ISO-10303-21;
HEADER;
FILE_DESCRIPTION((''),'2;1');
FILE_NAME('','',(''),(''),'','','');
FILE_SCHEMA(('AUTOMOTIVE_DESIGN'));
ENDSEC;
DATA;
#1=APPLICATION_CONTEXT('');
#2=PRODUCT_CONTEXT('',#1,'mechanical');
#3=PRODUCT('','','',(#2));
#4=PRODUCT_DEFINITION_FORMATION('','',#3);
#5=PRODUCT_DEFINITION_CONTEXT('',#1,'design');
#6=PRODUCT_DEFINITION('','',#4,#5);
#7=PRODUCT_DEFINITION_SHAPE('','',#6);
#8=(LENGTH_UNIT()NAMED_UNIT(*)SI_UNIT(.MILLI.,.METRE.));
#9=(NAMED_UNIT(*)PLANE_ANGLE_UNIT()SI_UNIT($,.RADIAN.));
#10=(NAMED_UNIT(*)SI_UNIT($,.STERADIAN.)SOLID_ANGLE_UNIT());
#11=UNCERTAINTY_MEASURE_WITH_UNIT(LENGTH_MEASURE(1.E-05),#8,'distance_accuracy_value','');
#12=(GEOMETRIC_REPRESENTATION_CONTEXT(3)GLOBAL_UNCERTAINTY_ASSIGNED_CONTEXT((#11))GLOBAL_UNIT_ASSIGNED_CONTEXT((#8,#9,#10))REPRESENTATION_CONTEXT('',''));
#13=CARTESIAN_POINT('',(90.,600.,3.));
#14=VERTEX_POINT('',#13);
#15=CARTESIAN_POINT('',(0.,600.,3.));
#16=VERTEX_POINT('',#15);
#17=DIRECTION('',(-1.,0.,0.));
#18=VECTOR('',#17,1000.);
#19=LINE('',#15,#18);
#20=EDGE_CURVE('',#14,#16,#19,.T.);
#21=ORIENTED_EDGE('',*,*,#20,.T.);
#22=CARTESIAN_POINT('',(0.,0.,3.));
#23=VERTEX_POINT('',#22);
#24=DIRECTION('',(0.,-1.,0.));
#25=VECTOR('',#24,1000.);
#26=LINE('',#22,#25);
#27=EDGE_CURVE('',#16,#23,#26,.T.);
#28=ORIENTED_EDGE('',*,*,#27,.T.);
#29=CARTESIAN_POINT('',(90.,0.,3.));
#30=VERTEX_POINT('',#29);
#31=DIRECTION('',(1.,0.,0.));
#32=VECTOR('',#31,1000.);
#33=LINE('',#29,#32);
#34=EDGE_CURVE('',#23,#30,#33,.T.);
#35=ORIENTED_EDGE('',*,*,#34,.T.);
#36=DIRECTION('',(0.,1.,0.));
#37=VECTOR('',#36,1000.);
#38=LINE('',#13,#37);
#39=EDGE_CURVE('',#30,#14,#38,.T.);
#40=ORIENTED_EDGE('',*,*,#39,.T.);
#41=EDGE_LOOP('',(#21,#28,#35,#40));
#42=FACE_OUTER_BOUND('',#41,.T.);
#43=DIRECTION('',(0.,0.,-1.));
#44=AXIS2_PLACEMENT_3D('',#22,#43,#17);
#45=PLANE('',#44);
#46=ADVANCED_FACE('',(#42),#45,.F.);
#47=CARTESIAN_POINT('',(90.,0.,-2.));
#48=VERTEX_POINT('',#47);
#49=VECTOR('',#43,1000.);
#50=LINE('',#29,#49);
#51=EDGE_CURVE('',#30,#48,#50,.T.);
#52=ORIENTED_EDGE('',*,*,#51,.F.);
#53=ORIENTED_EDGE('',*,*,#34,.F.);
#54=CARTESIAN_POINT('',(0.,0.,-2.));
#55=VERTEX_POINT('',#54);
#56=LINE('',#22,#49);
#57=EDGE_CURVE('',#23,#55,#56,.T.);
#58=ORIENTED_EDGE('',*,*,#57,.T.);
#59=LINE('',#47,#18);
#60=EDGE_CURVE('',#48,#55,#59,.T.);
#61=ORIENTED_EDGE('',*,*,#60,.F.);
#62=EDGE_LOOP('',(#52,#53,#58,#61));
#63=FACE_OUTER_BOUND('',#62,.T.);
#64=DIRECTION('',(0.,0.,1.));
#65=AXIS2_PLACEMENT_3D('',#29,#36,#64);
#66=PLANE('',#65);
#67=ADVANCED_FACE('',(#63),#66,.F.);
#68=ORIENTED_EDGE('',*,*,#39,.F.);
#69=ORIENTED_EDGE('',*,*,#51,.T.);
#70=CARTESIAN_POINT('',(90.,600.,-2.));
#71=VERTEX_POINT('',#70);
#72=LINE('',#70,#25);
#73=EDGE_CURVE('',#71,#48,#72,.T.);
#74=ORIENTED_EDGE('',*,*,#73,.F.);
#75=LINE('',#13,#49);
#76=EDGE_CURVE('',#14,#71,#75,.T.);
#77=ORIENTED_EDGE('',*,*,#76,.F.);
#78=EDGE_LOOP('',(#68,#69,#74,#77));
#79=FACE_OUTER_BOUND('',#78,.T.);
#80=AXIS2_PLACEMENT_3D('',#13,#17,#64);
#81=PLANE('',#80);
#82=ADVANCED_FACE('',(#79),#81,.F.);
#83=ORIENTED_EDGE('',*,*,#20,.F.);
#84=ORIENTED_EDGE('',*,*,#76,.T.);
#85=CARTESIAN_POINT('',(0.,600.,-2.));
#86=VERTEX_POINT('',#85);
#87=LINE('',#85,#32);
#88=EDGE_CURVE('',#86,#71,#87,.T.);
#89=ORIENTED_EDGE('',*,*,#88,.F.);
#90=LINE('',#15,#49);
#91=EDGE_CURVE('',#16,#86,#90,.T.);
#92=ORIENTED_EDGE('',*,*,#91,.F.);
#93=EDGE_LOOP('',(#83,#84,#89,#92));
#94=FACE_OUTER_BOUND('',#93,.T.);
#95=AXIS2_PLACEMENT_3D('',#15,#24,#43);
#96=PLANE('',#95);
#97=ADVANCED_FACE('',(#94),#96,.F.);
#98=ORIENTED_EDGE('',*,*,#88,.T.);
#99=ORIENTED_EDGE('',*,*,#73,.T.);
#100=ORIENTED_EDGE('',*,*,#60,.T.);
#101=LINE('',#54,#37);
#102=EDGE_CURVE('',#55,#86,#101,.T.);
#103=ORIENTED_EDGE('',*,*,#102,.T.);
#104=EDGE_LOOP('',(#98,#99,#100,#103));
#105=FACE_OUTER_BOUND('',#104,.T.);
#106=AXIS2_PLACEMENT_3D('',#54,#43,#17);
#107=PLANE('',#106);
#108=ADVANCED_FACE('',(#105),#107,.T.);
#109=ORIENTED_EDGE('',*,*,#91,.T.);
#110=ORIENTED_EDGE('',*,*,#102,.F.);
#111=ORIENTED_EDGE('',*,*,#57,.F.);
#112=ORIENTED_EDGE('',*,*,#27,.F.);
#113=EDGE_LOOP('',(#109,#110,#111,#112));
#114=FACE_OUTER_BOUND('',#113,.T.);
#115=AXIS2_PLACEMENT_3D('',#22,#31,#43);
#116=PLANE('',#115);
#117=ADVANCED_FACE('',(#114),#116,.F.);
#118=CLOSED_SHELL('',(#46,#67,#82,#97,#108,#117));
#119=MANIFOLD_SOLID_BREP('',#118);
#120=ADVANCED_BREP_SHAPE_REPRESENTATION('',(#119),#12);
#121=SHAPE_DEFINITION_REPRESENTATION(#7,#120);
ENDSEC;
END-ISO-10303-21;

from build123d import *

# Parameters (mm, degrees)
SKETCH_1_W      = 90
SKETCH_1_H      = 600
EXTRUDE_1_DEPTH = 3
SKETCH_2_W      = 90
SKETCH_2_H      = 600
EXTRUDE_2_DEPTH = 2


with BuildPart() as part:
    # 草图1 → 凸台-拉伸1 (new body)
    with BuildSketch(Plane.XY):
        with Locations((45, 300)):
            Rectangle(SKETCH_1_W, SKETCH_1_H)
    extrude(amount=EXTRUDE_1_DEPTH)

    # 草图2 → 凸台-拉伸2 (add)
    with BuildSketch(Plane(origin=(0, 0, 0), x_dir=(-1, 0, 0), z_dir=(0, 0, -1))):
        with Locations((-45, 300)):
            Rectangle(SKETCH_2_W, SKETCH_2_H)
    extrude(amount=EXTRUDE_2_DEPTH)


solid = part.part
